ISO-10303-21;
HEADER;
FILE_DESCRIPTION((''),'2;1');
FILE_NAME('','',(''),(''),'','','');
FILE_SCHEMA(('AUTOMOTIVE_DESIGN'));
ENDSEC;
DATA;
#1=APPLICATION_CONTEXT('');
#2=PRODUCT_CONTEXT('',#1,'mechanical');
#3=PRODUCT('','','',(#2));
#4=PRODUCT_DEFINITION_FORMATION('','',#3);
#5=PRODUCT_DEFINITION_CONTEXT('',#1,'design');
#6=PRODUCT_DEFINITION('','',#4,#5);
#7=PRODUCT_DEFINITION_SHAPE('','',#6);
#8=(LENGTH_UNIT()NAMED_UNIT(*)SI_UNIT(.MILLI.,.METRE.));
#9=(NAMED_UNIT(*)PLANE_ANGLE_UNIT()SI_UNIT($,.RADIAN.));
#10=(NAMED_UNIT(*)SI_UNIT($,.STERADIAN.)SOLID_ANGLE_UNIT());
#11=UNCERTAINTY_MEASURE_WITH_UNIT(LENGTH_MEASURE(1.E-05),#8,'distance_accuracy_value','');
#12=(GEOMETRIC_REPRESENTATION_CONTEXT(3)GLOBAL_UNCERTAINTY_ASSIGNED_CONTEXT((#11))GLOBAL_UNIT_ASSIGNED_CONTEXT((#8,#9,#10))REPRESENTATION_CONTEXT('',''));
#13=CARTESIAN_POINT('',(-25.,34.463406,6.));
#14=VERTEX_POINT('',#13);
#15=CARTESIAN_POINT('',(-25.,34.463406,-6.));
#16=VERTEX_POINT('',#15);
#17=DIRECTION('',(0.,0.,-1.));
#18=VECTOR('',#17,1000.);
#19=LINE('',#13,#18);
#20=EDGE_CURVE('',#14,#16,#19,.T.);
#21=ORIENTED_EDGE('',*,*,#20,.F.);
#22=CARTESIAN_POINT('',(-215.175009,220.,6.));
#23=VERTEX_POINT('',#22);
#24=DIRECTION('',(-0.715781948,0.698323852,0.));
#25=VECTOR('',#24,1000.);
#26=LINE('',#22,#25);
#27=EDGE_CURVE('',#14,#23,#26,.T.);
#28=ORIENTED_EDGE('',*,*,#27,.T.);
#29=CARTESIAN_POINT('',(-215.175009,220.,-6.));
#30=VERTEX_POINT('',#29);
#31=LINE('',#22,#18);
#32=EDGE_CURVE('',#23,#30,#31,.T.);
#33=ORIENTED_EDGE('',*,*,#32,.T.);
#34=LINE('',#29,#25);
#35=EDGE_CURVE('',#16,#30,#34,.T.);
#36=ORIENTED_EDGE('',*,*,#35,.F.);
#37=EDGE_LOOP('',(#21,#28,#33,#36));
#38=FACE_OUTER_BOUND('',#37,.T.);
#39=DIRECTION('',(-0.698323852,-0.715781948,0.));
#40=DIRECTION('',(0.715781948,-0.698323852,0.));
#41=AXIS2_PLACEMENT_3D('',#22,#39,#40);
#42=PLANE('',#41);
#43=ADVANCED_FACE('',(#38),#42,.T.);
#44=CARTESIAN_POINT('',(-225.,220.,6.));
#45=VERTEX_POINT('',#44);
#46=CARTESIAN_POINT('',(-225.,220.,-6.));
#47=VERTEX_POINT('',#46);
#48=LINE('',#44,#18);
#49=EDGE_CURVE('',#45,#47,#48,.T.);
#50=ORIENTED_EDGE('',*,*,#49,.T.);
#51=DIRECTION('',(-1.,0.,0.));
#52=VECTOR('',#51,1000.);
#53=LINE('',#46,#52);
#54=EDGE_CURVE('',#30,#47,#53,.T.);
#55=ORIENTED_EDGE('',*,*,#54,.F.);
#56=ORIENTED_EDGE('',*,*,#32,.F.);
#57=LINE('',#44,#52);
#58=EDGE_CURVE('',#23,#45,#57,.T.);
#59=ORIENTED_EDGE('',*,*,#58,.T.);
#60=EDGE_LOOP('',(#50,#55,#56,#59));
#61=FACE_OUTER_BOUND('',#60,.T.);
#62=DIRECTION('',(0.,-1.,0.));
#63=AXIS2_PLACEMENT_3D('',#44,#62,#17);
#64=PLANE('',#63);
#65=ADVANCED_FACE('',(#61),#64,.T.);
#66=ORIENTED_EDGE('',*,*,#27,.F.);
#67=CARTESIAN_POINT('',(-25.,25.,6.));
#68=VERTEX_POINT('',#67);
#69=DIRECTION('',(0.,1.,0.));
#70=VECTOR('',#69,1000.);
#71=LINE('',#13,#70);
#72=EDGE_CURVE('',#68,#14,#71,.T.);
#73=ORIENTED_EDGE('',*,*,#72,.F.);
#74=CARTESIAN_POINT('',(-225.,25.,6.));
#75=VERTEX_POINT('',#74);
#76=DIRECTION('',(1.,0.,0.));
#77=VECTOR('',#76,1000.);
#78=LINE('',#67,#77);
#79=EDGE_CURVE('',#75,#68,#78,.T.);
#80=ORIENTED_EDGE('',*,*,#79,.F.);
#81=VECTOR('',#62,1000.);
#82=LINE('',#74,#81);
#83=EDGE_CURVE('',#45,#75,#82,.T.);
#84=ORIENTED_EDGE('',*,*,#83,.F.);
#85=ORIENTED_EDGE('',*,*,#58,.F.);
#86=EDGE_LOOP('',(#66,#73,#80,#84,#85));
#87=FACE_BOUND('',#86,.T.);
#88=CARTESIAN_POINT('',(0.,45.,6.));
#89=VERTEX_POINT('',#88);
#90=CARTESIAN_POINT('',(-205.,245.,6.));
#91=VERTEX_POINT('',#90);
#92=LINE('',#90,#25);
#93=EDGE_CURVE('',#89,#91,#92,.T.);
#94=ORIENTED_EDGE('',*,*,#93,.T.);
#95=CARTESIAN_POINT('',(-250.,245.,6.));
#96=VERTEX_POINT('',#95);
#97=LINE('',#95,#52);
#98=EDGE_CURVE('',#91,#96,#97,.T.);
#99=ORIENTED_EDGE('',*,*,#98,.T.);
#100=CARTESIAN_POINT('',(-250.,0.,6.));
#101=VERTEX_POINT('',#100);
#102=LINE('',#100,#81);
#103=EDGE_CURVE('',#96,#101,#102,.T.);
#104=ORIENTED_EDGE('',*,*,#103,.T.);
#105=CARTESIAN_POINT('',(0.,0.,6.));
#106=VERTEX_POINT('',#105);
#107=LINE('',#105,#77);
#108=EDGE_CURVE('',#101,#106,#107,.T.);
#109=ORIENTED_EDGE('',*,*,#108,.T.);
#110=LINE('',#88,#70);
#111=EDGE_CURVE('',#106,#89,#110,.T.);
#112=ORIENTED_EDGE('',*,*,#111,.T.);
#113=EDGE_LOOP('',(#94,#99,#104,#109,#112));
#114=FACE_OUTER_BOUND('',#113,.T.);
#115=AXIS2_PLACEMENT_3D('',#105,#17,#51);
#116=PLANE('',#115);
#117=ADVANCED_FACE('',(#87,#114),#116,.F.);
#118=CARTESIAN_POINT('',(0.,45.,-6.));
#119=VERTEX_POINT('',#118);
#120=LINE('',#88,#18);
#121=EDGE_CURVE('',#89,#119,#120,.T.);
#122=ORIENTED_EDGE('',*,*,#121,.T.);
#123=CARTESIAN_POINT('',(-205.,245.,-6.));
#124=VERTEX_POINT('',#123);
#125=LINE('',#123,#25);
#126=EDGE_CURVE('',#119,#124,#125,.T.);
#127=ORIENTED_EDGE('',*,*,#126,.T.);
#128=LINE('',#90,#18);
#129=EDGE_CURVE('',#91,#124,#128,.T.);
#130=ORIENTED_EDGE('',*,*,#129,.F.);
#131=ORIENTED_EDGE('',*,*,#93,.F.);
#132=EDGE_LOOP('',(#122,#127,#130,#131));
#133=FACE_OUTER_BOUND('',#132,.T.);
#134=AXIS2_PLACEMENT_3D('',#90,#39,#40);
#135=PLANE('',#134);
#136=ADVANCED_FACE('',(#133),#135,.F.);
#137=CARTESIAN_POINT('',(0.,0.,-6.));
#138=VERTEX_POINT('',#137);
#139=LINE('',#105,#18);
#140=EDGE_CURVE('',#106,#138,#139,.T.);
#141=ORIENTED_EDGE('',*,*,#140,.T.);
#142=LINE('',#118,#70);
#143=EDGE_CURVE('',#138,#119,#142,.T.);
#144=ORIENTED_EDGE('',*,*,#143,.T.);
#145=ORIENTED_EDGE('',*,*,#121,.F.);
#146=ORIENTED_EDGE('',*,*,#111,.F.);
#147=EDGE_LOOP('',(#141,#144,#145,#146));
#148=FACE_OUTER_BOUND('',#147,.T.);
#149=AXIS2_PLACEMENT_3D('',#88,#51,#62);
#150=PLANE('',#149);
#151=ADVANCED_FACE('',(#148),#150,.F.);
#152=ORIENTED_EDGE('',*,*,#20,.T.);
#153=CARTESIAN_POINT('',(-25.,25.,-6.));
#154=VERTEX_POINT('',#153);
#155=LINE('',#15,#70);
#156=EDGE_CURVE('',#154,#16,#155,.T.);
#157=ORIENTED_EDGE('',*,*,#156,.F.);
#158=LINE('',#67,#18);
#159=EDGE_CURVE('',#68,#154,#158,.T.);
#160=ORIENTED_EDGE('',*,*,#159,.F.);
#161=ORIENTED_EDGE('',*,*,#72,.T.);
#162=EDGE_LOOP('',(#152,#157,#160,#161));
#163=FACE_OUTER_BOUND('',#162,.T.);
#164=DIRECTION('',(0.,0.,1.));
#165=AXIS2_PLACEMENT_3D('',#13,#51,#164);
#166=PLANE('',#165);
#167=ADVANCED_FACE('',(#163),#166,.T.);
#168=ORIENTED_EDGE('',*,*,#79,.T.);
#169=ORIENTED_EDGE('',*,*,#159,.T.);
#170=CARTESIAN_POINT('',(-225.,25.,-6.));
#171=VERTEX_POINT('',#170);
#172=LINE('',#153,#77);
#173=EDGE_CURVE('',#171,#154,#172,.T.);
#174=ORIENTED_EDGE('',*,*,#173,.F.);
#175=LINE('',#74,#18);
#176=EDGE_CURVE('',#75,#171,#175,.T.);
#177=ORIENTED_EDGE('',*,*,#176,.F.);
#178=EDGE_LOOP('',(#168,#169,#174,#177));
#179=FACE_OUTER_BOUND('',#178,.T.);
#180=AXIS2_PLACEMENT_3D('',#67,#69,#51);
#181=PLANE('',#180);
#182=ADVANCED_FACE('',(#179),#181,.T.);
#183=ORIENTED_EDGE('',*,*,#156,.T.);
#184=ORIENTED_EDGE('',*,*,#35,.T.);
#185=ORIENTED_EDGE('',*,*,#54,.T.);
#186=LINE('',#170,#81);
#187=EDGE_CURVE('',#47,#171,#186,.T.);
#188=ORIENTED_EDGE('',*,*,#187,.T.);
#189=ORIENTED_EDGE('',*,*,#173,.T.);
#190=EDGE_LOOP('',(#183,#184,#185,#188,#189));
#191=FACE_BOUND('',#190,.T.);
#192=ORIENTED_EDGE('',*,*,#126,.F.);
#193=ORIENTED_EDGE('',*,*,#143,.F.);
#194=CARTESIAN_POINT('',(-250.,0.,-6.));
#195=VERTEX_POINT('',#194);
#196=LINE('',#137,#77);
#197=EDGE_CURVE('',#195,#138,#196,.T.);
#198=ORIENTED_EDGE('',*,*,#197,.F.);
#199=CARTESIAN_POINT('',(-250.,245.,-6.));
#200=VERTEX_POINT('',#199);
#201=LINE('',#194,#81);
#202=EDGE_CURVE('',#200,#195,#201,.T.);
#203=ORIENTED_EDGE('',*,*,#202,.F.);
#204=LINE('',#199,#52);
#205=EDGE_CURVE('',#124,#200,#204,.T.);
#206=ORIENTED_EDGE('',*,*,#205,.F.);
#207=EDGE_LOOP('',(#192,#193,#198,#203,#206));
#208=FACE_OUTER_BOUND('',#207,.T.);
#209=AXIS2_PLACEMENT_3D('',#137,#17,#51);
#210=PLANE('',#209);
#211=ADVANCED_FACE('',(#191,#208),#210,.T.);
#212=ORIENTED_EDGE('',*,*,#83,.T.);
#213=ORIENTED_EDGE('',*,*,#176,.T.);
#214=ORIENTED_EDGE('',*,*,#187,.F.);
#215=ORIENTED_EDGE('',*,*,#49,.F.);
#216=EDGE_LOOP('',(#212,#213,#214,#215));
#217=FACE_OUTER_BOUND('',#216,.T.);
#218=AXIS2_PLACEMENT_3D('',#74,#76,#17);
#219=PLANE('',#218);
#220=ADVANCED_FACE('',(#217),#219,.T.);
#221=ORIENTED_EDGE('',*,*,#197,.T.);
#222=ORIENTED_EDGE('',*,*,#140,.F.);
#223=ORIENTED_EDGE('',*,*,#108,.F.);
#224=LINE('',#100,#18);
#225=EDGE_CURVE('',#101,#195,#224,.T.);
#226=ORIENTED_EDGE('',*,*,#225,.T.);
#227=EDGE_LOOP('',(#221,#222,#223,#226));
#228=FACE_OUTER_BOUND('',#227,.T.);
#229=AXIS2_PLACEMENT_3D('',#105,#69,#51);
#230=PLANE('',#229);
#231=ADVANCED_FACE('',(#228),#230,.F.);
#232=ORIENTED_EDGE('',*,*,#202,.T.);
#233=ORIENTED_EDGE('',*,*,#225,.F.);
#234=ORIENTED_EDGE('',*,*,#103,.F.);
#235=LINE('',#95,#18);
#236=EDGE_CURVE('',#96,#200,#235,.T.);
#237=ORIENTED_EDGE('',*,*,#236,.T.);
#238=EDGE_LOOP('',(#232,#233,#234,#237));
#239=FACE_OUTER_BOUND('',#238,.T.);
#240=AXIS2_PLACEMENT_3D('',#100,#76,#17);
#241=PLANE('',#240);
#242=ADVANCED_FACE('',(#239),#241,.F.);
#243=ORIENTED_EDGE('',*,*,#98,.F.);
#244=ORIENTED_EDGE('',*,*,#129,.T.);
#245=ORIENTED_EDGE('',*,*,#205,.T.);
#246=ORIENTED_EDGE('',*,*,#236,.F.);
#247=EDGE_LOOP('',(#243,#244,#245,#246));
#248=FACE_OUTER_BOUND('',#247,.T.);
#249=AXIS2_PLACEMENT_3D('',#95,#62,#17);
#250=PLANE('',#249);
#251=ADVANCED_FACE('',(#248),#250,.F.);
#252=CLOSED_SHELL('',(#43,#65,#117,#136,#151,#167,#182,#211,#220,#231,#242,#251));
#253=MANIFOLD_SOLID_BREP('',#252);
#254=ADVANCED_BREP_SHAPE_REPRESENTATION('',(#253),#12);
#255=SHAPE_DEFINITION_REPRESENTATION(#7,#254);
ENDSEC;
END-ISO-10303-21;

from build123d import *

# Parameters (mm, degrees)
EXTRUDE_1_DEPTH = 6


with BuildPart() as part:
    # 草图1 → 凸台-拉伸1 (new, symmetric)
    with BuildSketch(Plane.XY):
        Polygon((0, 0), (-250, 0), (-250, 245), (-205, 245), (0, 45), align=None)
        Polygon((-225, 220), (-215.175008729, 220), (-25, 34.463406118), (-25, 25), (-225, 25), align=None, mode=Mode.SUBTRACT)
    extrude(amount=EXTRUDE_1_DEPTH, both=True)


solid = part.part
